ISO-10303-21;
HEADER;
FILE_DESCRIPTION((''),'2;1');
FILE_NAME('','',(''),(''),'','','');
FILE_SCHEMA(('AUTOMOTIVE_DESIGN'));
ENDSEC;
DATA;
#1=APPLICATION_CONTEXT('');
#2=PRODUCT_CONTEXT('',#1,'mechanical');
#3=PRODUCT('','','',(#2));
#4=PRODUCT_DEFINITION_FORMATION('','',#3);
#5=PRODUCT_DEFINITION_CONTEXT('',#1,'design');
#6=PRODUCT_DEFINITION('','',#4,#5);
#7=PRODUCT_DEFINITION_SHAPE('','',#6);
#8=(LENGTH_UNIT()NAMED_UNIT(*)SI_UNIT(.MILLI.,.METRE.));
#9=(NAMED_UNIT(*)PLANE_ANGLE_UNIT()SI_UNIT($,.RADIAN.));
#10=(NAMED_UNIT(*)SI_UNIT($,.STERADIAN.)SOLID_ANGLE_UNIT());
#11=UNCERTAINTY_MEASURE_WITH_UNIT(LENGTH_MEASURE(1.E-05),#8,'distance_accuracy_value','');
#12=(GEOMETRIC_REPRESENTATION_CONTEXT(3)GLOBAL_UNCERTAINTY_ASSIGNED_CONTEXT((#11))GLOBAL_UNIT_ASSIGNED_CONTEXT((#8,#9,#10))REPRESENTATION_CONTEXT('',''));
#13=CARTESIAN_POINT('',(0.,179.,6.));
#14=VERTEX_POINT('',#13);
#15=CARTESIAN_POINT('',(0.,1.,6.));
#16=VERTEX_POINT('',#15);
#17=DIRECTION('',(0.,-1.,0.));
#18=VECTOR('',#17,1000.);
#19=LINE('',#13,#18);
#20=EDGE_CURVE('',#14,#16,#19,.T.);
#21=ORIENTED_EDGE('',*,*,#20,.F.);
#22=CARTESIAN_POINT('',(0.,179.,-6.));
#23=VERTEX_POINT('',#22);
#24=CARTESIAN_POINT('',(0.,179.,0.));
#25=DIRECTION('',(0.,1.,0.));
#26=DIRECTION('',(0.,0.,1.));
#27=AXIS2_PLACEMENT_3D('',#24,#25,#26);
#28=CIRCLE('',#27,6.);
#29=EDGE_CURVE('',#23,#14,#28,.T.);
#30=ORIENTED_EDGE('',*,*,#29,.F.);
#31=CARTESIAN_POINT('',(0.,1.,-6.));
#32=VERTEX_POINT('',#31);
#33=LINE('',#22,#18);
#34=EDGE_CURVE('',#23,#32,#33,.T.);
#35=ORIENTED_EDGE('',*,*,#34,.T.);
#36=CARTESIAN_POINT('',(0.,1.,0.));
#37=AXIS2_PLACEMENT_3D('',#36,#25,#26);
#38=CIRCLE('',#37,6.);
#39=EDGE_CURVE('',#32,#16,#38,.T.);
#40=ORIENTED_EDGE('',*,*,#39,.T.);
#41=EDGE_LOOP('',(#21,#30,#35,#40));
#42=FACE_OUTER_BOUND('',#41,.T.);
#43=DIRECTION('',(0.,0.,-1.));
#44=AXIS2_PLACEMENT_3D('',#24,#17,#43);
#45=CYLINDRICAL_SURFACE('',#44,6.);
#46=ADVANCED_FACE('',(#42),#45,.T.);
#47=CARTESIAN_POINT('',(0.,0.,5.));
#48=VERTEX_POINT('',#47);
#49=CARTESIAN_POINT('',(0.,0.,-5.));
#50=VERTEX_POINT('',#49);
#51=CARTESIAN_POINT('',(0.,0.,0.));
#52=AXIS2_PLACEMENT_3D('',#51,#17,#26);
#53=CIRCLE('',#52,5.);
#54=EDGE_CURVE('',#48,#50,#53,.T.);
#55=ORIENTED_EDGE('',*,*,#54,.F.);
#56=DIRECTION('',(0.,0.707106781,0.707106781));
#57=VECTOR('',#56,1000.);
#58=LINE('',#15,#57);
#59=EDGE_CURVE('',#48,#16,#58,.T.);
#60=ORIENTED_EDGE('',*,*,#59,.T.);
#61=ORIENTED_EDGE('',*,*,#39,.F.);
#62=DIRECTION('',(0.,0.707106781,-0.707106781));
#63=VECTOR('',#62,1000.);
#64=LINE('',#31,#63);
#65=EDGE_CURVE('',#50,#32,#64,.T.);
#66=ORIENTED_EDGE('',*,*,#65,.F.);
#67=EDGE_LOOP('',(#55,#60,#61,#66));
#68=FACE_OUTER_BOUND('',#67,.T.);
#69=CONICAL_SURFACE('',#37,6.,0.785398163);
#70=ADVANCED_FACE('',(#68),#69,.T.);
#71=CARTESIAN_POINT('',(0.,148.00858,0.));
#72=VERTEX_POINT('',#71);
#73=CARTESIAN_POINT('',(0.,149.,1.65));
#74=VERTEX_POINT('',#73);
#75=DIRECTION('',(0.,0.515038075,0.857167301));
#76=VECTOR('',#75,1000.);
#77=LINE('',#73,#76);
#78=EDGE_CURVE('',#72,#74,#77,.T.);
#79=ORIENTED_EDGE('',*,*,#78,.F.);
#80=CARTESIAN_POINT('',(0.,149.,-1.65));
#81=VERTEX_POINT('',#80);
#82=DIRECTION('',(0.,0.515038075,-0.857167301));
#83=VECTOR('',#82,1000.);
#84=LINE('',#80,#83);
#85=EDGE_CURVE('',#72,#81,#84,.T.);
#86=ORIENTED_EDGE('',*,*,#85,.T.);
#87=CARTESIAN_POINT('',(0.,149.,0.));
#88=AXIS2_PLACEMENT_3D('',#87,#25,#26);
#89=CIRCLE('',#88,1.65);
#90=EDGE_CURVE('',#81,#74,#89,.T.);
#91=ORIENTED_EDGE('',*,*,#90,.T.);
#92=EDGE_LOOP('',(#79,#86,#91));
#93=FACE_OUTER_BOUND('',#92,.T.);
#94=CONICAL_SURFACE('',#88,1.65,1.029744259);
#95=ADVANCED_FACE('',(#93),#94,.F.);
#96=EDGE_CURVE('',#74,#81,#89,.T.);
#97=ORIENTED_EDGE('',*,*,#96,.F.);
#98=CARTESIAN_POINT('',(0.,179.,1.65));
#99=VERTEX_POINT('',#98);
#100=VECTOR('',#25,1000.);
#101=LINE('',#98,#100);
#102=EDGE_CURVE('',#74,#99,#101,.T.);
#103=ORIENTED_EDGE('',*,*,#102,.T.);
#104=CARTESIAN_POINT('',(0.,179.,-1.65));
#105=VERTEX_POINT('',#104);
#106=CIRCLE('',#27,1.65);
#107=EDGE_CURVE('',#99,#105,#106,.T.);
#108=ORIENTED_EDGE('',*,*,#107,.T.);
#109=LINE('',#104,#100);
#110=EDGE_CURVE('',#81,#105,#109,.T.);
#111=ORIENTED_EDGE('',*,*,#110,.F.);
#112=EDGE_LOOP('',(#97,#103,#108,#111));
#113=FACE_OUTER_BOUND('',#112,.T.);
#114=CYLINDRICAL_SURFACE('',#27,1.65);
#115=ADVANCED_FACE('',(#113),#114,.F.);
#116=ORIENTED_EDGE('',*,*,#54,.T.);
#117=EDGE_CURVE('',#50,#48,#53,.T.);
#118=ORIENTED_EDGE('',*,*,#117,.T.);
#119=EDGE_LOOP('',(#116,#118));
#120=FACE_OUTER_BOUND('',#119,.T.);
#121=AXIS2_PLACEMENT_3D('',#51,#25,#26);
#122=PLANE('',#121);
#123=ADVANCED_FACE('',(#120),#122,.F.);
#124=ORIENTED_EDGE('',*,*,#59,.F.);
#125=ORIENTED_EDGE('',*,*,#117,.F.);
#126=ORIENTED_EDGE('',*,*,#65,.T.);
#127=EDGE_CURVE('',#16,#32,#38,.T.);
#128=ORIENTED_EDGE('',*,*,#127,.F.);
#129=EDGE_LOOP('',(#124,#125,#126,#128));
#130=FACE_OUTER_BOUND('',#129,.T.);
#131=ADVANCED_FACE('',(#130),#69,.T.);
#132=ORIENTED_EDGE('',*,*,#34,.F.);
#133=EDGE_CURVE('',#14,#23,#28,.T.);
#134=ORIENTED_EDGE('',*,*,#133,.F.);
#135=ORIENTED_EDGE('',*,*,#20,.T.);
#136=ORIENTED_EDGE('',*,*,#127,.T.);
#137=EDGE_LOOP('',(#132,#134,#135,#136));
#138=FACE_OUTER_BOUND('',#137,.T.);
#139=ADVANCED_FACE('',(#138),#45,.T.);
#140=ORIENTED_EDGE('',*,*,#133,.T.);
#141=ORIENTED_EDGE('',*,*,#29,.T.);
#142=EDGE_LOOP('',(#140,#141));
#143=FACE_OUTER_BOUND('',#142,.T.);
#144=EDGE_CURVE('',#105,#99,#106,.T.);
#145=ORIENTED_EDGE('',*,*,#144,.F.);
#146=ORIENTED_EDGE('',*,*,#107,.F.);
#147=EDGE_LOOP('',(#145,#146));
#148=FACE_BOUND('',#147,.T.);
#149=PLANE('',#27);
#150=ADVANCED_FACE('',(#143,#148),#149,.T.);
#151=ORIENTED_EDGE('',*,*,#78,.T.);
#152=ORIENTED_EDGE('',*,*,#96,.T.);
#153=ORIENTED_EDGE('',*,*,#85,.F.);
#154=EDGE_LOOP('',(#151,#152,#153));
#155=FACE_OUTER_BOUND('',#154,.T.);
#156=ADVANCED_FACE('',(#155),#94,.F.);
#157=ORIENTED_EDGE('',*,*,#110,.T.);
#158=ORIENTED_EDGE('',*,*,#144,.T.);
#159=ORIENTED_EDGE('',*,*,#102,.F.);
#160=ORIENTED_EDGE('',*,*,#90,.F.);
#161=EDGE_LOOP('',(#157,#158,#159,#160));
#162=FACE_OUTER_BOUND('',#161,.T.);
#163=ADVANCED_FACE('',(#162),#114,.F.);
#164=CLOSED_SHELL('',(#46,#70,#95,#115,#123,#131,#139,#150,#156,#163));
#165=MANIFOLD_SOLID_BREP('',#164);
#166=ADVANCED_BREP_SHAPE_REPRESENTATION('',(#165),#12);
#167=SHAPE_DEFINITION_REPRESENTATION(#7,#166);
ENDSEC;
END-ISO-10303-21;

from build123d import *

# Parameters (mm, degrees)
SKETCH1_R             = 6
BOSS_EXTRUDE1_DEPTH   = 179
M4_TAPPED_HOLE1_D     = 3.3
M4_TAPPED_HOLE1_DEPTH = 30
M4_TAPPED_HOLE1_TIP   = 0.991420021
CHAMFER1_SIZE         = 1


with BuildPart() as part:
    # Sketch1 → Boss-Extrude1 (new body)
    with BuildSketch(Plane(origin=(0, 0, 0), x_dir=(1, 0, 0), z_dir=(0, 1, 0))):
        with Locations(Location((0, 0, 0), (0, 0, 90))):
            Circle(SKETCH1_R)
    extrude(amount=BOSS_EXTRUDE1_DEPTH)

    # M4 Tapped Hole1
    with Locations(Plane(origin=(0, 179, 0), x_dir=(1, 0, 0), z_dir=(0, 1, 0))):
        with Locations((0, 0), (-123.257585015, 97.244885399), (-195.107309259, 6.175586916), (-71.849724244, -91.069298483)):
            Hole(M4_TAPPED_HOLE1_D / 2, depth=M4_TAPPED_HOLE1_DEPTH)
            with Locations((0, 0, -(M4_TAPPED_HOLE1_DEPTH + M4_TAPPED_HOLE1_TIP / 2))):  # 118° drill point
                Cone(0, M4_TAPPED_HOLE1_D / 2, M4_TAPPED_HOLE1_TIP, mode=Mode.SUBTRACT)

    # Chamfer1
    chamfer1_edges = [part.edges().sort_by_distance(p)[0] for p in [
        (0, 0, 6),
    ]]
    chamfer(chamfer1_edges, length=CHAMFER1_SIZE)


solid = part.part
